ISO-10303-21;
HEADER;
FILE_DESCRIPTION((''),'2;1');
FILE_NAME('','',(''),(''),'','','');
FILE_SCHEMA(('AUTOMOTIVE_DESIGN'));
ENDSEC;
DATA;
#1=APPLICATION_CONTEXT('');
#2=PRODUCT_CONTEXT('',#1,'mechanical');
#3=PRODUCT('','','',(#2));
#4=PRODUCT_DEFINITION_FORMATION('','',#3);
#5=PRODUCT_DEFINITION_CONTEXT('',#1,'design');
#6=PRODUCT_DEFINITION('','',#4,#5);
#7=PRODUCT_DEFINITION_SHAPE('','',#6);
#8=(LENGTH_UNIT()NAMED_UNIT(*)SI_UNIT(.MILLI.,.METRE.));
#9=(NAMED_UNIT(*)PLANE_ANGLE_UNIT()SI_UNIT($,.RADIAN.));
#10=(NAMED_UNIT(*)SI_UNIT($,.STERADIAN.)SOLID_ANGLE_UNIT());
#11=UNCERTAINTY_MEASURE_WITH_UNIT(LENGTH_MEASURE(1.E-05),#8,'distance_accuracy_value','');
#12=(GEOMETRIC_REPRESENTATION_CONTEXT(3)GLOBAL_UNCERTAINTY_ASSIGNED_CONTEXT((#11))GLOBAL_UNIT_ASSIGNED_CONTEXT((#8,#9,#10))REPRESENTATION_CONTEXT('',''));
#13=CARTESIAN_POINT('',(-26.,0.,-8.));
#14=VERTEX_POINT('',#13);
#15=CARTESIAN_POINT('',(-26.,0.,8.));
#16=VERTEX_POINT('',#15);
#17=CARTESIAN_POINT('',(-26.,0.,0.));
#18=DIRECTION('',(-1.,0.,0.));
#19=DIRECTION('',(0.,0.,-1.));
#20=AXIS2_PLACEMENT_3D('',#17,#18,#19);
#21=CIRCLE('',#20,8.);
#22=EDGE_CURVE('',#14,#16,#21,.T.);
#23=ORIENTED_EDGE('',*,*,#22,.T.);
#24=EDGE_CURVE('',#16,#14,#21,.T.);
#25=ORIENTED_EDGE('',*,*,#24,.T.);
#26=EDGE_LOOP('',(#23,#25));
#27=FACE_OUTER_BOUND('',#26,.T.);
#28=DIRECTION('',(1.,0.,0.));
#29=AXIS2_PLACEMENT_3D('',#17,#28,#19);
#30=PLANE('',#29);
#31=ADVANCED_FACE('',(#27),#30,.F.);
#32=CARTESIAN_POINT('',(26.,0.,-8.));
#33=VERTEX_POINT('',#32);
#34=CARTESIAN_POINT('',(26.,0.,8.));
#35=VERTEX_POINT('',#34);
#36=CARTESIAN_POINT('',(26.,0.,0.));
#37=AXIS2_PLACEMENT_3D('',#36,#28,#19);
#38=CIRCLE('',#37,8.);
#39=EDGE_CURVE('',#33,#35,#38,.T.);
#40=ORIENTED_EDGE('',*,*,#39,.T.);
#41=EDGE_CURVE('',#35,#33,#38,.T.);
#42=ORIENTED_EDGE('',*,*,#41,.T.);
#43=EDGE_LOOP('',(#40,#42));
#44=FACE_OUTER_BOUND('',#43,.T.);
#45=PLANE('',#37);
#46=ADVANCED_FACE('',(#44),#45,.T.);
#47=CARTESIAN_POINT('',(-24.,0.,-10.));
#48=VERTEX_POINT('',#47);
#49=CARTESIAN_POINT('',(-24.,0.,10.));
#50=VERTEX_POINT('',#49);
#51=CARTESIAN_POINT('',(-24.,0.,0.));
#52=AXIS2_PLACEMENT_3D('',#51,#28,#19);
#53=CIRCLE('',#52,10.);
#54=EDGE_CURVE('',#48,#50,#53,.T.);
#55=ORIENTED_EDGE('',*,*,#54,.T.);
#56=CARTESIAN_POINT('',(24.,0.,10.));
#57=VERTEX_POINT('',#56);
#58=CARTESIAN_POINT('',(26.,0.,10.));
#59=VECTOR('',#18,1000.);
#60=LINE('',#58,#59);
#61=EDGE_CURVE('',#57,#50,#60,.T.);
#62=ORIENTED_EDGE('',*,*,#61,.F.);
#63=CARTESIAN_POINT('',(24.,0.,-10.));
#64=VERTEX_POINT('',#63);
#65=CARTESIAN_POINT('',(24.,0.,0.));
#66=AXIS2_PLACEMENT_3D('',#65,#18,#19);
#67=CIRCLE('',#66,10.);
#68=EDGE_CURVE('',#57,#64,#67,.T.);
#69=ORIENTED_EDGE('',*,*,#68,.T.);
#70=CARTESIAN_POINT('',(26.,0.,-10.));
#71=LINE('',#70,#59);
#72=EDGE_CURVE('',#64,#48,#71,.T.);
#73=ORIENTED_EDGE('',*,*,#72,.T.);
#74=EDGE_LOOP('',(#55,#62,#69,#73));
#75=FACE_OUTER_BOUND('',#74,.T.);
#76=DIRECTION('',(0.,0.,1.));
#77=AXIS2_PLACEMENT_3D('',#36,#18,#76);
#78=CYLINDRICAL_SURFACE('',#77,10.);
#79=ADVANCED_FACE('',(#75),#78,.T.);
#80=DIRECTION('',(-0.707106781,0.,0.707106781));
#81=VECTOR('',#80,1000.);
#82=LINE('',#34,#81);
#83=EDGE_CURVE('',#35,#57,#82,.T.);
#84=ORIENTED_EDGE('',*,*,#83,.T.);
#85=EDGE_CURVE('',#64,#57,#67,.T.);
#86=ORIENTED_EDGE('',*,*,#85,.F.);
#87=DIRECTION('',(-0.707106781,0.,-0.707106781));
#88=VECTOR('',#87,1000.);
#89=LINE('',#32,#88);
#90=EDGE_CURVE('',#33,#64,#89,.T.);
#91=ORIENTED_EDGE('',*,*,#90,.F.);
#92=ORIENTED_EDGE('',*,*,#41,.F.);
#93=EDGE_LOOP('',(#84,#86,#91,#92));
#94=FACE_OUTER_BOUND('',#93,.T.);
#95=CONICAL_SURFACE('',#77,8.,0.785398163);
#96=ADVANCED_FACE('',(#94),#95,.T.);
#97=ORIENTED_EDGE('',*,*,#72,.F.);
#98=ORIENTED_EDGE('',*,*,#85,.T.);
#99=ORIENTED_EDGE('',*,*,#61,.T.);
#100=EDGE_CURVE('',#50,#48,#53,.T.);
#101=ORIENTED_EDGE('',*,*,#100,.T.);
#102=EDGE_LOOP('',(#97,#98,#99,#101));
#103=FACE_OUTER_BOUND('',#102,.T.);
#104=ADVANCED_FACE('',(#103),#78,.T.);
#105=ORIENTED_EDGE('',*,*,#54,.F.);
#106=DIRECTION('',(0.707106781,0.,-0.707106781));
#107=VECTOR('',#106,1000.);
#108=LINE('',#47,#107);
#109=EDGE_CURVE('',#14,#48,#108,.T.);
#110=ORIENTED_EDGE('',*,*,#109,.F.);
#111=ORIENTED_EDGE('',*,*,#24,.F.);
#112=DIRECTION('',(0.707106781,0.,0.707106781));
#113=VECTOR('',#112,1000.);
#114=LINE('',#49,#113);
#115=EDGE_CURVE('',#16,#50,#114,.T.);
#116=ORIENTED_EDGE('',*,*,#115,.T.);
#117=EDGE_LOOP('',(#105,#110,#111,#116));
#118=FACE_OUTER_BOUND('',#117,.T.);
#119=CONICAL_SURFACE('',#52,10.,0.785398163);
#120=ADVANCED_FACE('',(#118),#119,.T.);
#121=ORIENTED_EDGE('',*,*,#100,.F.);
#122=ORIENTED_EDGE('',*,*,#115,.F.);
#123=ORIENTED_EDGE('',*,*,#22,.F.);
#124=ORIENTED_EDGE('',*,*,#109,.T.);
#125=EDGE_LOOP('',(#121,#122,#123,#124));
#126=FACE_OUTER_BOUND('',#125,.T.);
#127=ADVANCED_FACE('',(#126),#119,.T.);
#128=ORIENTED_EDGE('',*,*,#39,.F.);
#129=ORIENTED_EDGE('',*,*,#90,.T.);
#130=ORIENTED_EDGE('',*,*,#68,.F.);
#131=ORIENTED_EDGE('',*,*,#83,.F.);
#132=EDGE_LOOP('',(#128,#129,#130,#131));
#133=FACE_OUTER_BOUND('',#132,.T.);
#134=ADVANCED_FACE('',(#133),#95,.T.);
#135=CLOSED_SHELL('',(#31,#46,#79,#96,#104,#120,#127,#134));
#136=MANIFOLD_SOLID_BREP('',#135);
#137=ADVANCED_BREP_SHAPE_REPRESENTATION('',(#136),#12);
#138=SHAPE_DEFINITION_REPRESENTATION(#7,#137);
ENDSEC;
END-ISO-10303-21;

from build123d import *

# Parameters (mm, degrees)
PIN_PROFILE_20_R       = 10
PIN_BODY_20X52_DEPTH   = 26
END_CHAMFERS_2X45_SIZE = 2


with BuildPart() as part:
    # Pin Profile Ø20 → Pin Body Ø20x52 (new, symmetric)
    with BuildSketch(Plane(origin=(0, 0, 0), x_dir=(0, 0, -1), z_dir=(1, 0, 0))):
        with Locations(Location((0, 0, 0), (0, 0, 180))):
            Circle(PIN_PROFILE_20_R)
    extrude(amount=PIN_BODY_20X52_DEPTH, both=True)

    # End Chamfers 2x45°
    end_chamfers_2x45_edges = [part.edges().sort_by_distance(p)[0] for p in [
        (-26, 0, -10),
        (26, 0, -10),
    ]]
    chamfer(end_chamfers_2x45_edges, length=END_CHAMFERS_2X45_SIZE)


solid = part.part
